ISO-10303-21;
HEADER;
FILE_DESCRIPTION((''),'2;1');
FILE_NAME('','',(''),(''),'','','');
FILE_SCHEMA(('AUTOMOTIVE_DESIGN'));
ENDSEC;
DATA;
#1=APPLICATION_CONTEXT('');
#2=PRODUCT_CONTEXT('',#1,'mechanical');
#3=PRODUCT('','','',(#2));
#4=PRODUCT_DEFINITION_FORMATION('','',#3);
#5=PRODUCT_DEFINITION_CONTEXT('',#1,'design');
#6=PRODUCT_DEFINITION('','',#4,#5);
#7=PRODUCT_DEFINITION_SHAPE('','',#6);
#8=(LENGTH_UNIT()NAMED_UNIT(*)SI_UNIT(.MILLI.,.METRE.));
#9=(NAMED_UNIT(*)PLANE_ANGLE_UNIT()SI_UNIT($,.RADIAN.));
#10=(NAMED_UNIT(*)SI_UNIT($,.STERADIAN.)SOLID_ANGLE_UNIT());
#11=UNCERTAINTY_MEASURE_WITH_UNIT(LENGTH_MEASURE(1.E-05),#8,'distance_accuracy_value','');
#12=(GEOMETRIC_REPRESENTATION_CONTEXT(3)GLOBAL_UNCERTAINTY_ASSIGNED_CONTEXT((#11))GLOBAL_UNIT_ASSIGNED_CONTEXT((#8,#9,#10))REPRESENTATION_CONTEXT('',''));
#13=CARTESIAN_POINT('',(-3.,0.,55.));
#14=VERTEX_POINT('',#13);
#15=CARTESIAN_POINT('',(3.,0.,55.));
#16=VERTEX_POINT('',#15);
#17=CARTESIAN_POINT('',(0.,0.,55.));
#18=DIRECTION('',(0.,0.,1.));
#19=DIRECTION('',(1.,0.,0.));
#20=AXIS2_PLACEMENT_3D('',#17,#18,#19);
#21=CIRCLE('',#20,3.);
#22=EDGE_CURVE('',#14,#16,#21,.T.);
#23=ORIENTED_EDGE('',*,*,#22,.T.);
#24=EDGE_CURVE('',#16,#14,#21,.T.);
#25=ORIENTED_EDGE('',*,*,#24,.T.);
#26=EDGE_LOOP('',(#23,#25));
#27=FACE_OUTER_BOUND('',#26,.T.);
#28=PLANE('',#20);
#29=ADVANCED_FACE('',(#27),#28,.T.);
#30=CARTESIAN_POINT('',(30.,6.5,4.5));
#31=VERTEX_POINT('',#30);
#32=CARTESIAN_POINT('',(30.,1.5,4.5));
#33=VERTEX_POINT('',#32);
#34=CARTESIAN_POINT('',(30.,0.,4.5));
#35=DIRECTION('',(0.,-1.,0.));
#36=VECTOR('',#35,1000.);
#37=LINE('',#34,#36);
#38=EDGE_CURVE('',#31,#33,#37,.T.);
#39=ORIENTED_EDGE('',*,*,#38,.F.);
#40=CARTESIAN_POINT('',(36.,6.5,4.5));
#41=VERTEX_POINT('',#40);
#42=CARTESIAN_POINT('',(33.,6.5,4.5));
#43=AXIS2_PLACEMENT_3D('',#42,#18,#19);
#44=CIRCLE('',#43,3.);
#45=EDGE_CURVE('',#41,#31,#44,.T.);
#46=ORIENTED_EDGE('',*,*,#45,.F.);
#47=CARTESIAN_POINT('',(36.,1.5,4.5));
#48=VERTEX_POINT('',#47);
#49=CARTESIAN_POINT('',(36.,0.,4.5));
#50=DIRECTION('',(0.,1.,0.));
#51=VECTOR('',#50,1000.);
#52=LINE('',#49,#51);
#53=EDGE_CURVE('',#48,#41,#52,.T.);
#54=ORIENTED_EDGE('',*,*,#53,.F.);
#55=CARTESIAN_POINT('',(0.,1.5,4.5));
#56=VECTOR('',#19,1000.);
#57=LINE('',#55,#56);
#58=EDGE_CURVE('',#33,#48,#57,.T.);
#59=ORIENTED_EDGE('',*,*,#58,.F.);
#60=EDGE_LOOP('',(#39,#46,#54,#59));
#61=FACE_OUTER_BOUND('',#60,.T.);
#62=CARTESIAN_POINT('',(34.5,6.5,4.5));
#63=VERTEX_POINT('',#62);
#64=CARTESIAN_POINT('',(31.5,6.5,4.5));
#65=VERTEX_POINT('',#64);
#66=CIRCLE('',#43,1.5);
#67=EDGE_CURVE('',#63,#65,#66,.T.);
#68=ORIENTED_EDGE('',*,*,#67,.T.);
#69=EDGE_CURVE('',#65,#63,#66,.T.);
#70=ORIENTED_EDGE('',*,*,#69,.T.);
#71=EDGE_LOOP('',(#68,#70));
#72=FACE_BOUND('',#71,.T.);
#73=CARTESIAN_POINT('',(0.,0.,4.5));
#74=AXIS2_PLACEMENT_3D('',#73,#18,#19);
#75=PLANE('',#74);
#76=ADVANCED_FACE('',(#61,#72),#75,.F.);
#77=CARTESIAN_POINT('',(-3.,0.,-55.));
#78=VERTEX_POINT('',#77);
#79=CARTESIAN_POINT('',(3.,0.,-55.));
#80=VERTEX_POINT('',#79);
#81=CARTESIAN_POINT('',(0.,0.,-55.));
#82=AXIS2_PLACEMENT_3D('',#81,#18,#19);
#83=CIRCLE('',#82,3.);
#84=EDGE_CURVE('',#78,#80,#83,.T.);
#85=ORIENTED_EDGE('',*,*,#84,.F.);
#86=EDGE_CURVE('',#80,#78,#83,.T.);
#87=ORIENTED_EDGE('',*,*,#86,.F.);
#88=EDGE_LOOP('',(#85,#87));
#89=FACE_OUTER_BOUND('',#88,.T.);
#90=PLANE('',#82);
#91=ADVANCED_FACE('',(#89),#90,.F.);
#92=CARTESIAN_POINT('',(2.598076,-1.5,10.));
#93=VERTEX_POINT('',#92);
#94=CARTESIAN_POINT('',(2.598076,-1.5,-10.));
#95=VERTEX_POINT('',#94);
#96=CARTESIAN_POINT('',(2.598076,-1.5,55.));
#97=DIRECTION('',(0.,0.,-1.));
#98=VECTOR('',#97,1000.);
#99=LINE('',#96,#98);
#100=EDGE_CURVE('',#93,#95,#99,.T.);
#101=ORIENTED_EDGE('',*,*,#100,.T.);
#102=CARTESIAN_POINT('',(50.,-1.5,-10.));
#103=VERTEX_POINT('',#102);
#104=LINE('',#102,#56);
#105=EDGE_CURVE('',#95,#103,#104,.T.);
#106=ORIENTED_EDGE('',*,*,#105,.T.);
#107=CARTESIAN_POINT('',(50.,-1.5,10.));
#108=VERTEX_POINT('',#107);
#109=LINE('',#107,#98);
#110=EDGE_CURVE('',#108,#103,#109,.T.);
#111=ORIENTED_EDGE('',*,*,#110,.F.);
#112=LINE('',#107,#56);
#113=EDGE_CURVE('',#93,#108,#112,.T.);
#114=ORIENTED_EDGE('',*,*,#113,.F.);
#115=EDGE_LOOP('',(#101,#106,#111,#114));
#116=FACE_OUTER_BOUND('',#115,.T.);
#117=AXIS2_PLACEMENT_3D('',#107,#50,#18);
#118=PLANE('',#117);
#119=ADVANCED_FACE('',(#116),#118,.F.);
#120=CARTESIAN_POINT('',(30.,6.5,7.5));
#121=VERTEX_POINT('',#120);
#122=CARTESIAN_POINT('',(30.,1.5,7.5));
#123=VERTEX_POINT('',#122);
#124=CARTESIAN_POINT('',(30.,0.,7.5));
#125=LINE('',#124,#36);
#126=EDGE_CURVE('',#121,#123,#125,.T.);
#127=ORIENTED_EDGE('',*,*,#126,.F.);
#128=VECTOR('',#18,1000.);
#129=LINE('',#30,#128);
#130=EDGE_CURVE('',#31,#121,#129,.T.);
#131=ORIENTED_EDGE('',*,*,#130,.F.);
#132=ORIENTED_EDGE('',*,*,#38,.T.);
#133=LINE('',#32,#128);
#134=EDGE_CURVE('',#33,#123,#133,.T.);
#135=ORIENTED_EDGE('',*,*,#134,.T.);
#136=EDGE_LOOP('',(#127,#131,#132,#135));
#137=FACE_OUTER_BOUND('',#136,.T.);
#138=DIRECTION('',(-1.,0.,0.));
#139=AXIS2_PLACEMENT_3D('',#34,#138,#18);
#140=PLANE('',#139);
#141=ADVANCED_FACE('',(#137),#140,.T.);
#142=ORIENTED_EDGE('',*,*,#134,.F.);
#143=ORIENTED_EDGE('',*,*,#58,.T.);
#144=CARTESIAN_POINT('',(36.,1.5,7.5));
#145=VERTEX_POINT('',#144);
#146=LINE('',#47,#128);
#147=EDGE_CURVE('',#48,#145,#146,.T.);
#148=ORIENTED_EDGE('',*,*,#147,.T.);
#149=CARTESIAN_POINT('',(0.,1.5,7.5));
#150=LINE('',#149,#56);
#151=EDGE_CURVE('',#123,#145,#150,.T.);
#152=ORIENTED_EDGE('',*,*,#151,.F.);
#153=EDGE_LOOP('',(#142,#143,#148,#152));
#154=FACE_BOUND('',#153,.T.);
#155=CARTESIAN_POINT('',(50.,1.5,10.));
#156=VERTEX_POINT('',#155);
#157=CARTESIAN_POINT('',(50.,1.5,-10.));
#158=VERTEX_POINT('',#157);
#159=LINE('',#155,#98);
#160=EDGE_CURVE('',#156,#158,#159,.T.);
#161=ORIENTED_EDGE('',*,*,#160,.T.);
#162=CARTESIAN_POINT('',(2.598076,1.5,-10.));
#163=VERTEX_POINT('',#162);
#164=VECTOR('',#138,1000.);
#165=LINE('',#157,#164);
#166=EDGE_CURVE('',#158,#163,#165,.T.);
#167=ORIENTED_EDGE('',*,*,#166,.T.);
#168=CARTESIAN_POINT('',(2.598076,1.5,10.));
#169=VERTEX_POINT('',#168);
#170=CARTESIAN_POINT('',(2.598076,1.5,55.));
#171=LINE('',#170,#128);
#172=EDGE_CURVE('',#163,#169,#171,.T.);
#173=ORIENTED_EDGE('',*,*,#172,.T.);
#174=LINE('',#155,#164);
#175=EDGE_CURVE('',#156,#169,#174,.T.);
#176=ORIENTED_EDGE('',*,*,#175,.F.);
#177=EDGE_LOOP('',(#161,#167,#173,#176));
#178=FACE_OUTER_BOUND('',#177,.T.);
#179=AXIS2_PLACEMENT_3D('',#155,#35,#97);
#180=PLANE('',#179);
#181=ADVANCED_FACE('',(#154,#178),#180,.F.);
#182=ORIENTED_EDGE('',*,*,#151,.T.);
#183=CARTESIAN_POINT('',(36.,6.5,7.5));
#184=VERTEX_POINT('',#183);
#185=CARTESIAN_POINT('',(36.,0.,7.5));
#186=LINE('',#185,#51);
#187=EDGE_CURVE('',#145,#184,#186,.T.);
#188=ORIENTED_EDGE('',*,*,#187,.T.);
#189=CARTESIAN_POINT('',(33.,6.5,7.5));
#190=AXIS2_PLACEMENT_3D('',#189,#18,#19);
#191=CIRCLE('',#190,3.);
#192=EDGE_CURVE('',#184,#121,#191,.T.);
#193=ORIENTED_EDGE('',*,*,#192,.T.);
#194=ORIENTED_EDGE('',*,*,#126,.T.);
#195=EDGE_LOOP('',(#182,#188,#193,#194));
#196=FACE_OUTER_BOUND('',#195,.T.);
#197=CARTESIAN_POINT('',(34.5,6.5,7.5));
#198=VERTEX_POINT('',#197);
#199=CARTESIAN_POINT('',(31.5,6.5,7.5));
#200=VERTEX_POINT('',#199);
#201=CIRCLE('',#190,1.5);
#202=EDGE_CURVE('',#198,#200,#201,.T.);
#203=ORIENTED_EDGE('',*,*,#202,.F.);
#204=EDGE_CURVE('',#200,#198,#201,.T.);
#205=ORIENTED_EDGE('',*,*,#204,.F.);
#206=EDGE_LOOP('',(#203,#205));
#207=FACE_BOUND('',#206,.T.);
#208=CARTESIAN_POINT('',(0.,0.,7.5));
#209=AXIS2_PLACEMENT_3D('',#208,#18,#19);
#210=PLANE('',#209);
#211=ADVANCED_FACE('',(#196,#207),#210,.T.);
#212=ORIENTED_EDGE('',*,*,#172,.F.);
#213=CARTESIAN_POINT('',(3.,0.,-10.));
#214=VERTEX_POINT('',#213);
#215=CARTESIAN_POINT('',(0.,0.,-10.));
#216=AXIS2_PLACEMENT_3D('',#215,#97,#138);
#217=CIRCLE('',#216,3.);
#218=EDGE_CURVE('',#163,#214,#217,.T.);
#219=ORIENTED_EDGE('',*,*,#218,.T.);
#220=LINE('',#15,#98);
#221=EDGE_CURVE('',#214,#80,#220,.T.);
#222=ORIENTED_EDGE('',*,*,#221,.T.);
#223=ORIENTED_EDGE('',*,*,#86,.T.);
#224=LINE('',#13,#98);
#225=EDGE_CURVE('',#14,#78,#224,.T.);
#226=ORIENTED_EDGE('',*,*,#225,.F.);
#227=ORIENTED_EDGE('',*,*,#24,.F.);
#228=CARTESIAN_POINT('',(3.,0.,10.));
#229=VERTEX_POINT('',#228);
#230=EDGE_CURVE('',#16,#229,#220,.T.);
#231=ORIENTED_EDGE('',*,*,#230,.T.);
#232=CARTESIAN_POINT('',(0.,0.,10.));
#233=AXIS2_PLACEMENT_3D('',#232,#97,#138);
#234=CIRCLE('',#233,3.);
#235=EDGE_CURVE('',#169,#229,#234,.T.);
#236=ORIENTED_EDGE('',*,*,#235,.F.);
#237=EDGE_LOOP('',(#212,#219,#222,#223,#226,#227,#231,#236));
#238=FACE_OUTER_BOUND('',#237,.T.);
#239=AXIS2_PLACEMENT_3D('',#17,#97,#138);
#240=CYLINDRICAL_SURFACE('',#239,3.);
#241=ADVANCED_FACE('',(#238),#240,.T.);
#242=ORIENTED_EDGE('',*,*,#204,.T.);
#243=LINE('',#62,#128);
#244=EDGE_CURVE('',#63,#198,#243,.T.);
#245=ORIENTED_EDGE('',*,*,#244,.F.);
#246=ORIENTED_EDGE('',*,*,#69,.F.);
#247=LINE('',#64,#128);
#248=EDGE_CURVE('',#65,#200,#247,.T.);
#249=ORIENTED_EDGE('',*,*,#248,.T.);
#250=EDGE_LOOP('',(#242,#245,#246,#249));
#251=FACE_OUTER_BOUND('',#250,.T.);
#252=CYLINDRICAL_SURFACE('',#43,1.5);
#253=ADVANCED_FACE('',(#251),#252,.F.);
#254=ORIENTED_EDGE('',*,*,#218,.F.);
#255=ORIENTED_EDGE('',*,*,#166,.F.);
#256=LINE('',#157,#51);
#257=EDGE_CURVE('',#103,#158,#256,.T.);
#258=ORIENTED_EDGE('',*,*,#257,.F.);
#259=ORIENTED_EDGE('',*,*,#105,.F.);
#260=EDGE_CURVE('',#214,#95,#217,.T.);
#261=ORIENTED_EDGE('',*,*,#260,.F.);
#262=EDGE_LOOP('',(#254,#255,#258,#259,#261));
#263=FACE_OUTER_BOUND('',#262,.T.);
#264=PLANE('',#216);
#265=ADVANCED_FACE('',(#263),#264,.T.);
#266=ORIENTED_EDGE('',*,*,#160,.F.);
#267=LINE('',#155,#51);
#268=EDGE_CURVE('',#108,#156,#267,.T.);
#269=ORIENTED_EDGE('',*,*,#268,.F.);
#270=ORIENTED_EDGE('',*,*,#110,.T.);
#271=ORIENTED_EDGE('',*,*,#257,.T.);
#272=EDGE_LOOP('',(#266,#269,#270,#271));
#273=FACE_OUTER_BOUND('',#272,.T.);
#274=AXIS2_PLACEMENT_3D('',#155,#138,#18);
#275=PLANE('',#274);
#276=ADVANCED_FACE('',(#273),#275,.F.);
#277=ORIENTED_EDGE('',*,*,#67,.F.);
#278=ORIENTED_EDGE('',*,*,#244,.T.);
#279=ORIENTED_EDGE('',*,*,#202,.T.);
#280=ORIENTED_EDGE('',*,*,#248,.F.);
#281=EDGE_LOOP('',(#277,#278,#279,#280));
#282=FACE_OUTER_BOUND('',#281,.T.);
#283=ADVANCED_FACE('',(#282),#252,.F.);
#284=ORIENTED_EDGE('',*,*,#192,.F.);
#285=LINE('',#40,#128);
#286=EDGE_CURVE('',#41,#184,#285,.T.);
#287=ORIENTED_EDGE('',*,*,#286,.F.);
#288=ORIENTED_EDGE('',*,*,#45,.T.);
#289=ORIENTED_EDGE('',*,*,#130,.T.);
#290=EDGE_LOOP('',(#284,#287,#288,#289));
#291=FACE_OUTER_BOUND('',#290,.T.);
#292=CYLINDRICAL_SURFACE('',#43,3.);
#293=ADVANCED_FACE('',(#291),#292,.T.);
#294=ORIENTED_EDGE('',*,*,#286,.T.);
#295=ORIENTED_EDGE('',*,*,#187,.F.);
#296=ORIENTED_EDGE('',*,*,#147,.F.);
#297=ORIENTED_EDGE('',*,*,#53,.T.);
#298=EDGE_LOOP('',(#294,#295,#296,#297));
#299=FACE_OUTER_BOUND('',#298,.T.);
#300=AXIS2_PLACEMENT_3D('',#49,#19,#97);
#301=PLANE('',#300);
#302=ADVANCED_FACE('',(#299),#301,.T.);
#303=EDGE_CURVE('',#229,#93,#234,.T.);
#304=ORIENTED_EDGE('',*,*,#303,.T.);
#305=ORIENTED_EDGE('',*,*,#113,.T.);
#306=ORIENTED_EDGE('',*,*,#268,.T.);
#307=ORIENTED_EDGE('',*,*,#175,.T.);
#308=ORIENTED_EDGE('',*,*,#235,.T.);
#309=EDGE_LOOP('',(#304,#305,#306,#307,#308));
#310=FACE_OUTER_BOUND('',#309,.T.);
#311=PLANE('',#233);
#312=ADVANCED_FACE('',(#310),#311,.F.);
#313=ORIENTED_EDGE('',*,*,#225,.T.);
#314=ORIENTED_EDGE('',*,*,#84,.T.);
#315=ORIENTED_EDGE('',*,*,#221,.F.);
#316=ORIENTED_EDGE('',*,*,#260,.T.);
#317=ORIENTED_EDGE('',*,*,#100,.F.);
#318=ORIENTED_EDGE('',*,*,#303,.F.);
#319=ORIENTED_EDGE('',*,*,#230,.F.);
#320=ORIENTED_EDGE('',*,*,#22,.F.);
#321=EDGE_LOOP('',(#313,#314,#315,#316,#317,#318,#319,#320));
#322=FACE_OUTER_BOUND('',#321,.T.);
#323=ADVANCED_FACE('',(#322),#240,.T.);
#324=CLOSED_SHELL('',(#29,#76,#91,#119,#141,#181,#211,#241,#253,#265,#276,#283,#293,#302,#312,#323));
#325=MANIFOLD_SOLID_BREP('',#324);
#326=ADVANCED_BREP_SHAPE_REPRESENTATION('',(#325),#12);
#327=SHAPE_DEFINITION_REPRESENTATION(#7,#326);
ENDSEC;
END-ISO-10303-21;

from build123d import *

# Parameters (mm, degrees)
SKETCH1_R           = 3
BOSS_EXTRUDE1_DEPTH = 55
SKETCH2_W           = 50
SKETCH2_H           = 3
BOSS_EXTRUDE2_DEPTH = 10
SKETCH3_R           = 3
SKETCH3_R_2         = 1.5
BOSS_EXTRUDE3_DEPTH = 3


with BuildPart() as part:
    # Sketch1 → Boss-Extrude1 (new, symmetric)
    with BuildSketch(Plane.XY):
        Circle(SKETCH1_R)
    extrude(amount=BOSS_EXTRUDE1_DEPTH, both=True)

    # Sketch2 → Boss-Extrude2 (add, symmetric)
    with BuildSketch(Plane.XY):
        with Locations((25, 0)):
            Rectangle(SKETCH2_W, SKETCH2_H)
    extrude(amount=BOSS_EXTRUDE2_DEPTH, both=True)

    # Sketch3 → Boss-Extrude3 (add)
    # profile 1 of 2: a face of its own
    with BuildSketch(Plane.XY.offset(7.5)):
        with Locations((33, 6.5)):
            Circle(SKETCH3_R)
        with Locations((33, 6.5)):
            Circle(SKETCH3_R_2, mode=Mode.SUBTRACT)
    # profile 2 of 2: a face of its own
    with BuildSketch(Plane.XY.offset(7.5)):
        with BuildLine():
            ThreePointArc((36, 6.5), (33, 3.5), (30, 6.5))
            Line((30, 6.5), (30, 1.5))
            Line((30, 1.5), (36, 1.5))
            Line((36, 1.5), (36, 6.5))
        make_face()
    extrude(amount=-BOSS_EXTRUDE3_DEPTH)


solid = part.part
